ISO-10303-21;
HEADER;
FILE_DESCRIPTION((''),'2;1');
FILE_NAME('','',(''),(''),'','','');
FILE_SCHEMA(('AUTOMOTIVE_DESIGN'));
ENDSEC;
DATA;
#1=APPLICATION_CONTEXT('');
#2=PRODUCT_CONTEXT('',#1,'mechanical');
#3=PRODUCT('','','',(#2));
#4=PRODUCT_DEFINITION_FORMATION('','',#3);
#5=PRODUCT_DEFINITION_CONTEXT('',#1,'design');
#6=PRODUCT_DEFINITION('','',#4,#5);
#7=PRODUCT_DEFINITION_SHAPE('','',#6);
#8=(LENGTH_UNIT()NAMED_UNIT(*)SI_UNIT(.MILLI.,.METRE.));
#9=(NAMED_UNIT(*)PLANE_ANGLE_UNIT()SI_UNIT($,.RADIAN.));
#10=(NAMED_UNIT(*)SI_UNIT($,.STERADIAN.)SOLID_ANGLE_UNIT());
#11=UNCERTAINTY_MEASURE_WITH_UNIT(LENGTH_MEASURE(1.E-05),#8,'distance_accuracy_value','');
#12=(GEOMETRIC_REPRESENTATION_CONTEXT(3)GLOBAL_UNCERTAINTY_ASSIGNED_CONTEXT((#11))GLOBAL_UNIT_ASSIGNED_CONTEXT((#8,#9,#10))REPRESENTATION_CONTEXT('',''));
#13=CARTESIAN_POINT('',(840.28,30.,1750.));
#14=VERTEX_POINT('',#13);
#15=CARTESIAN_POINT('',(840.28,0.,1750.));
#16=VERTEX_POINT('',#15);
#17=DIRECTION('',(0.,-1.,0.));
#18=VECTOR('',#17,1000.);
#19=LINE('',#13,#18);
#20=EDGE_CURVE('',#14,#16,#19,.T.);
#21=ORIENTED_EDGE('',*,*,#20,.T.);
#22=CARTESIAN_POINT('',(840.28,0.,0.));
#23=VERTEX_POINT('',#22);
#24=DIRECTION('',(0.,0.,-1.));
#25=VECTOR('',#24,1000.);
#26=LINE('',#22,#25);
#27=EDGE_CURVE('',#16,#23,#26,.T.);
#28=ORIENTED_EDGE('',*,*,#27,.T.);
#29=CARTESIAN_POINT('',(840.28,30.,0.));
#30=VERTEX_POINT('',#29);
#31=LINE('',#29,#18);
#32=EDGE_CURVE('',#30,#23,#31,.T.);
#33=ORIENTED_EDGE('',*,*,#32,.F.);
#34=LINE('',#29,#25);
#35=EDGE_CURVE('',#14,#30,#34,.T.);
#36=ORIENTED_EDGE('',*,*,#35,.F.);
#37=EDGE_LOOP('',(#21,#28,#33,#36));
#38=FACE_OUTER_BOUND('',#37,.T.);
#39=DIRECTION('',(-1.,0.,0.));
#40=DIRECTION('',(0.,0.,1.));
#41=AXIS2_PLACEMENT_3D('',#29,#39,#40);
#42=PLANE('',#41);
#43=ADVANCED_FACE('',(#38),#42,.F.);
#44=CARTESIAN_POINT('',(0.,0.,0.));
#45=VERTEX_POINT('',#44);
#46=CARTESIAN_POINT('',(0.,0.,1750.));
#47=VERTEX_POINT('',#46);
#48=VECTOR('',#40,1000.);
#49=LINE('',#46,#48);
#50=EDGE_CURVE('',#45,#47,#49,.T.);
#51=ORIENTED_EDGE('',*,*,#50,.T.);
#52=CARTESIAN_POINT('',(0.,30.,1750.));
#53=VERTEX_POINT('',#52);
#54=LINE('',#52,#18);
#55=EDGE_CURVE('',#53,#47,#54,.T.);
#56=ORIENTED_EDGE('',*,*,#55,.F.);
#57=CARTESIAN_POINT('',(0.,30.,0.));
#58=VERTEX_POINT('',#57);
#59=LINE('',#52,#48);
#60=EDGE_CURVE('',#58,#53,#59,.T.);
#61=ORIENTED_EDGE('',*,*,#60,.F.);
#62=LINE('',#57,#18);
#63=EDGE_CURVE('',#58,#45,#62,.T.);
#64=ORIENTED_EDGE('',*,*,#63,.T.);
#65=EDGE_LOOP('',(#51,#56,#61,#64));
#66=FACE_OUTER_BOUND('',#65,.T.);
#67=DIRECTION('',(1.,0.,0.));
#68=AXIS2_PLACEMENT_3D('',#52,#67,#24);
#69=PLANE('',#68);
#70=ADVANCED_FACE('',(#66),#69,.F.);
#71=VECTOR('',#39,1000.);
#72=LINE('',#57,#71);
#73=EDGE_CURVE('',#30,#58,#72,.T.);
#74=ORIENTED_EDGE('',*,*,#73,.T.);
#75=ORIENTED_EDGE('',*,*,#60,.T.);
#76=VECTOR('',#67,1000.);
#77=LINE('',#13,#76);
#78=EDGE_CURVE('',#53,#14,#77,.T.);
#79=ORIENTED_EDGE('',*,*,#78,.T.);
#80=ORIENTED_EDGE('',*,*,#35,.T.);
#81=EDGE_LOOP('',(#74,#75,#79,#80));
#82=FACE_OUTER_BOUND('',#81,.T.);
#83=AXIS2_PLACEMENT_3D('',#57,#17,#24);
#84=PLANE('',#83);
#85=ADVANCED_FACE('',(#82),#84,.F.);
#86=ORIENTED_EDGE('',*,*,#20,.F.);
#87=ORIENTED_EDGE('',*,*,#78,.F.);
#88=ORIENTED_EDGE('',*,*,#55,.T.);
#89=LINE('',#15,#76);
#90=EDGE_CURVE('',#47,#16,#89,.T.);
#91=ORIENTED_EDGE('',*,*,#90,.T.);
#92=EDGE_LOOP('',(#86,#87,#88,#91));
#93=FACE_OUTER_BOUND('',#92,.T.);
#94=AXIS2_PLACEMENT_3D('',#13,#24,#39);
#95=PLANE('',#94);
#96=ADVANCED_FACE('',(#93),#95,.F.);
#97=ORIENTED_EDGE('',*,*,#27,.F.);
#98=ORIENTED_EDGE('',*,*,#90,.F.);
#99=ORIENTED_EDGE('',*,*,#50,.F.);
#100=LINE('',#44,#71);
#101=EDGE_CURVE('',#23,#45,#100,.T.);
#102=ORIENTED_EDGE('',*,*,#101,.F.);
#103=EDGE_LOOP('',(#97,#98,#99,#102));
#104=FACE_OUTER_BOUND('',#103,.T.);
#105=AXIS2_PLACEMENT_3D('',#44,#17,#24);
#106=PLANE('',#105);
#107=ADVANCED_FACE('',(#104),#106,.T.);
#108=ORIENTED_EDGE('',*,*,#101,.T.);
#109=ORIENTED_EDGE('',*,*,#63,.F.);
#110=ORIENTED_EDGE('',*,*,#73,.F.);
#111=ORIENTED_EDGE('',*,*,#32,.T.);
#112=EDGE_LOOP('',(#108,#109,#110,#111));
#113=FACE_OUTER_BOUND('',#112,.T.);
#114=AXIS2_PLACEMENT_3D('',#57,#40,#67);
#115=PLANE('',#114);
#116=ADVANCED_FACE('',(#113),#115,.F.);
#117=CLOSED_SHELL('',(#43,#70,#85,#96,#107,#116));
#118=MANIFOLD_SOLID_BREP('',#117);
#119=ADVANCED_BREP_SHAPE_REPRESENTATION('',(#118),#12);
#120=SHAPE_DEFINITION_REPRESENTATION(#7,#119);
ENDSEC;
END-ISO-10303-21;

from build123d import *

# Parameters (mm, degrees)
SKETCH_1_W      = 840.28
SKETCH_1_H      = 1750
EXTRUDE_1_DEPTH = 30


with BuildPart() as part:
    # 草图1 → 凸台-拉伸1 (new body)
    with BuildSketch(Plane(origin=(0, 0, 0), x_dir=(1, 0, 0), z_dir=(0, 1, 0))):
        with Locations((420.14, -875)):
            Rectangle(SKETCH_1_W, SKETCH_1_H)
    extrude(amount=EXTRUDE_1_DEPTH)


solid = part.part
